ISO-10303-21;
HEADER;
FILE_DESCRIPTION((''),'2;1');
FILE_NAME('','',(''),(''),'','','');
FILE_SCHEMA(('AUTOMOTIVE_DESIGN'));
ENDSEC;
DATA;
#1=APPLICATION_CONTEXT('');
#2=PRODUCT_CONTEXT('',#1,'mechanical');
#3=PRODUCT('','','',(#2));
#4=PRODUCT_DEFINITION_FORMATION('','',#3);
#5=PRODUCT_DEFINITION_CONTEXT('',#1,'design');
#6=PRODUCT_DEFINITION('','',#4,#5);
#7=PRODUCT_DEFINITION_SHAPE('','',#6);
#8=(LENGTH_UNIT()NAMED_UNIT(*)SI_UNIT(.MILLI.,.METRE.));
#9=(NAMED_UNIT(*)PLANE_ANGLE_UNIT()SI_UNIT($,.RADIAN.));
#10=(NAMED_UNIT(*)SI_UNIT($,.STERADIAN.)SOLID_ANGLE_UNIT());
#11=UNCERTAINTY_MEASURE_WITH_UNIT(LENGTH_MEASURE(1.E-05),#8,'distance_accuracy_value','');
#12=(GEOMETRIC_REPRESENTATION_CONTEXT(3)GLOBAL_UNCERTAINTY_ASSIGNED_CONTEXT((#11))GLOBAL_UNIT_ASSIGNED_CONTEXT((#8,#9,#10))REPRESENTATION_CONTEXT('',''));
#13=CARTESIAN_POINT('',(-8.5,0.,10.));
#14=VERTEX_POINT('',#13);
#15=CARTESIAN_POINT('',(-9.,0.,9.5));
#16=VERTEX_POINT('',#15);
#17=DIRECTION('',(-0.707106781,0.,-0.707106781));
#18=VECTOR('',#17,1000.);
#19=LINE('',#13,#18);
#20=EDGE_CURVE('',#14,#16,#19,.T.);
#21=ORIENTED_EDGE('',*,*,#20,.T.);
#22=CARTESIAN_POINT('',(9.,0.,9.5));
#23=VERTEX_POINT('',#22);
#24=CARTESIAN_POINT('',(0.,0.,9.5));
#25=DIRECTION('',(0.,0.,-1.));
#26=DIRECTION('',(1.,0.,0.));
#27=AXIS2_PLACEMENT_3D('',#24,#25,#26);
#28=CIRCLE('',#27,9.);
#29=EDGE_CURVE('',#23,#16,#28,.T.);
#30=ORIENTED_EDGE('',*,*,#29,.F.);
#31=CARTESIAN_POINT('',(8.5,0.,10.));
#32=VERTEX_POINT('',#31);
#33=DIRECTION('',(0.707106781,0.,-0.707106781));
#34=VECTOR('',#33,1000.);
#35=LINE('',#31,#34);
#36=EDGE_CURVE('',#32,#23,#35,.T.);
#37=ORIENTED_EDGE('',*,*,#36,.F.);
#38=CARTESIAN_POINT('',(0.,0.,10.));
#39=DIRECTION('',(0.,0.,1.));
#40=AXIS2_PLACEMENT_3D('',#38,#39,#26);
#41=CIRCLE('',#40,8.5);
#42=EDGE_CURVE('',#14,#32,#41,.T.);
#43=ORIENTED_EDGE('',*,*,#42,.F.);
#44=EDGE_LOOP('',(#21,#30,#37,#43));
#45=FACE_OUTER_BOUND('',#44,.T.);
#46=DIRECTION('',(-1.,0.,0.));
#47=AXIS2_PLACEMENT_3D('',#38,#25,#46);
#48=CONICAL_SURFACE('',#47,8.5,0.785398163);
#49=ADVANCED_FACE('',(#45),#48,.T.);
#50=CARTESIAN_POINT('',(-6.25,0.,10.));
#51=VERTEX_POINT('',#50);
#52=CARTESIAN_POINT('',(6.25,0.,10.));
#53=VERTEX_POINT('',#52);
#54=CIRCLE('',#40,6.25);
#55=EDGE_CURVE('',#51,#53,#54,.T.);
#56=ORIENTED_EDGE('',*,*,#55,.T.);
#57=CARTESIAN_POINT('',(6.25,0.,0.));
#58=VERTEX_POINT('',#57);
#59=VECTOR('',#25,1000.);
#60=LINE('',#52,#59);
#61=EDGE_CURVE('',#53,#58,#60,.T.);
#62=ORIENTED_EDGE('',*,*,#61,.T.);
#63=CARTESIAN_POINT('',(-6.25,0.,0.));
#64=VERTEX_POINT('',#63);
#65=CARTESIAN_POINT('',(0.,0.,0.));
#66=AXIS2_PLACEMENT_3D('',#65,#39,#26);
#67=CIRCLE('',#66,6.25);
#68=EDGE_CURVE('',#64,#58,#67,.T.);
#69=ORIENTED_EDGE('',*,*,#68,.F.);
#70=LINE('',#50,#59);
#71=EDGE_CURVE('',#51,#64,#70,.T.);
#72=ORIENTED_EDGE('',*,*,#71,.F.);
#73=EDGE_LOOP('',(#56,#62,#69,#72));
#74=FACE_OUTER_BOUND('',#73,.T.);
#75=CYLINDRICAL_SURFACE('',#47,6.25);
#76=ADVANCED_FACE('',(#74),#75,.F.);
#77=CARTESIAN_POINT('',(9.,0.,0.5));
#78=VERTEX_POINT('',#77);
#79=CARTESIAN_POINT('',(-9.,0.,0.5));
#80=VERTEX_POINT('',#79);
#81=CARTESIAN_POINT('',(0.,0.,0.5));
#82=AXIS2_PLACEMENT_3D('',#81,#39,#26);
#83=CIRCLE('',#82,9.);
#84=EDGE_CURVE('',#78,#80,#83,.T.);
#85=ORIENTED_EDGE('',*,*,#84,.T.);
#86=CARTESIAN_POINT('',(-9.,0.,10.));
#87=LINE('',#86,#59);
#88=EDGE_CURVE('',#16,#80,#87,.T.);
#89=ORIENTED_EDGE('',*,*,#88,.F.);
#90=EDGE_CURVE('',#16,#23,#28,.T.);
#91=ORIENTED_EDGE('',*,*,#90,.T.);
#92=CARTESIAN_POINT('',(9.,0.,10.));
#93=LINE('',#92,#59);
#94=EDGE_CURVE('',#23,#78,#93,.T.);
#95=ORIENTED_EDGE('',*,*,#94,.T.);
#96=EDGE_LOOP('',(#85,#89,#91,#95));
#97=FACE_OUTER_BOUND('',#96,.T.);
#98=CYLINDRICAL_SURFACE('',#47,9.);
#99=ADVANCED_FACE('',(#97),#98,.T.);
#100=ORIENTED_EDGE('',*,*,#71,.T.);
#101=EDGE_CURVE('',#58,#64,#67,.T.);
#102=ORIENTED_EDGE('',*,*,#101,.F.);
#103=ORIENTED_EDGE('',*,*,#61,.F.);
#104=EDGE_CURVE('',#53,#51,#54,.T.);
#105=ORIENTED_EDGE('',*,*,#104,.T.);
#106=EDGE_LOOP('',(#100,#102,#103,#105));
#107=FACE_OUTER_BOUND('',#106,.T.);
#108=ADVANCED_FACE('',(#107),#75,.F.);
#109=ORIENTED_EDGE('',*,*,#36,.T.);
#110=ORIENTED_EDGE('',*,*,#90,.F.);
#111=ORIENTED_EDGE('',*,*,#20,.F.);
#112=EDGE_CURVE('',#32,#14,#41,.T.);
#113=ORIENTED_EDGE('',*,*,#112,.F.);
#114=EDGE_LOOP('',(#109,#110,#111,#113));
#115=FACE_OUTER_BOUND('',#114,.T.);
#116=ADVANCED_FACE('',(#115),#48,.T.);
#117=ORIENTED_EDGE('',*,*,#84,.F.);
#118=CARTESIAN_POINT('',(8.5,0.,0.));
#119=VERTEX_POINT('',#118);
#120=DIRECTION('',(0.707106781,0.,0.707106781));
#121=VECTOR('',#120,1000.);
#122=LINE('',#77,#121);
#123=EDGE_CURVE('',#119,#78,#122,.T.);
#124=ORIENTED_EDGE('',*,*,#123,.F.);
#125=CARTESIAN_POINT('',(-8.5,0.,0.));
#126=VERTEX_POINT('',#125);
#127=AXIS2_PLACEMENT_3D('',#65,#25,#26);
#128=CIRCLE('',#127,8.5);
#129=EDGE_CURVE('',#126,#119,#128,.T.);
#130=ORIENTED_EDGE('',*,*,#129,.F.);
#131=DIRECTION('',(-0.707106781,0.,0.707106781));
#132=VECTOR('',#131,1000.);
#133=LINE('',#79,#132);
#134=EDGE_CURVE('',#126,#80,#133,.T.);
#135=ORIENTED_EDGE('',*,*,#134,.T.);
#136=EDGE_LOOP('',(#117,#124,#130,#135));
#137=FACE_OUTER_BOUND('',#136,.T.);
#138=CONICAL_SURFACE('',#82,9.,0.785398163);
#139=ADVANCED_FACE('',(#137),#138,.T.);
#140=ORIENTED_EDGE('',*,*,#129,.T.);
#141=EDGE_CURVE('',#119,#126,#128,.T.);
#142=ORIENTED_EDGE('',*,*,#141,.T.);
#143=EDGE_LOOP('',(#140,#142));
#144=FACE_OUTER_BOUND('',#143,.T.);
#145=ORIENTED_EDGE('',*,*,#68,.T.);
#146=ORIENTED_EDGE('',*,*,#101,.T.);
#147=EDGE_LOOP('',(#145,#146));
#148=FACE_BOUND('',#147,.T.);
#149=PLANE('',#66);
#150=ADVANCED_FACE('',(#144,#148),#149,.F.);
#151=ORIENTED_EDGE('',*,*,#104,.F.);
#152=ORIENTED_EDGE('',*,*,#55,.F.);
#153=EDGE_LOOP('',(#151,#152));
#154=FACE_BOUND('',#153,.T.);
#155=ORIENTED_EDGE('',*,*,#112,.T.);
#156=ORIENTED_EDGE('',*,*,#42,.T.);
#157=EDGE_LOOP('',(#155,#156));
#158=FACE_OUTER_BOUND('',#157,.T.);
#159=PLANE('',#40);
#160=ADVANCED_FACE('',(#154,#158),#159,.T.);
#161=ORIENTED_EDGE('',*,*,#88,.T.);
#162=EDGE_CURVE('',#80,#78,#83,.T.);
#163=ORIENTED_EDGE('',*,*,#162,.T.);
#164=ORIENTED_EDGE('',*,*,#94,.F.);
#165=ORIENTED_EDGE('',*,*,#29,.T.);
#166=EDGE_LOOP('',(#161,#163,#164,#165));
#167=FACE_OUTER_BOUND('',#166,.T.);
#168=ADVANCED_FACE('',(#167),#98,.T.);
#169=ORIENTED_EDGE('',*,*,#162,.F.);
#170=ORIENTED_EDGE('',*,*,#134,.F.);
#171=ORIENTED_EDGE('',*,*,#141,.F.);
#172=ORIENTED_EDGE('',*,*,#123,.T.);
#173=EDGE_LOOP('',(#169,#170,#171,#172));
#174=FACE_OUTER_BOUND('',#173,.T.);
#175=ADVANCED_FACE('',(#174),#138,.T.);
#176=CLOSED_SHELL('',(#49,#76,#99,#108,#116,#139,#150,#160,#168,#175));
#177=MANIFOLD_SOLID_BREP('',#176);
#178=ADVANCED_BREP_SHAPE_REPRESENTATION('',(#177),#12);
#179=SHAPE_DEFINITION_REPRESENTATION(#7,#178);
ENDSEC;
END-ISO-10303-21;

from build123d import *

# Parameters (mm, degrees)
SKETCH1_R           = 9
SKETCH1_R_2         = 6.25
BOSS_EXTRUDE1_DEPTH = 10
CHAMFER1_SIZE       = 0.5


with BuildPart() as part:
    # Sketch1 → Boss-Extrude1 (new body)
    with BuildSketch(Plane.XY):
        Circle(SKETCH1_R)
        Circle(SKETCH1_R_2, mode=Mode.SUBTRACT)
    extrude(amount=BOSS_EXTRUDE1_DEPTH)

    # Chamfer1
    chamfer1_edges = [part.edges().sort_by_distance(p)[0] for p in [
        (-9, 0, 0),
        (-9, 0, 10),
    ]]
    chamfer(chamfer1_edges, length=CHAMFER1_SIZE)


solid = part.part
